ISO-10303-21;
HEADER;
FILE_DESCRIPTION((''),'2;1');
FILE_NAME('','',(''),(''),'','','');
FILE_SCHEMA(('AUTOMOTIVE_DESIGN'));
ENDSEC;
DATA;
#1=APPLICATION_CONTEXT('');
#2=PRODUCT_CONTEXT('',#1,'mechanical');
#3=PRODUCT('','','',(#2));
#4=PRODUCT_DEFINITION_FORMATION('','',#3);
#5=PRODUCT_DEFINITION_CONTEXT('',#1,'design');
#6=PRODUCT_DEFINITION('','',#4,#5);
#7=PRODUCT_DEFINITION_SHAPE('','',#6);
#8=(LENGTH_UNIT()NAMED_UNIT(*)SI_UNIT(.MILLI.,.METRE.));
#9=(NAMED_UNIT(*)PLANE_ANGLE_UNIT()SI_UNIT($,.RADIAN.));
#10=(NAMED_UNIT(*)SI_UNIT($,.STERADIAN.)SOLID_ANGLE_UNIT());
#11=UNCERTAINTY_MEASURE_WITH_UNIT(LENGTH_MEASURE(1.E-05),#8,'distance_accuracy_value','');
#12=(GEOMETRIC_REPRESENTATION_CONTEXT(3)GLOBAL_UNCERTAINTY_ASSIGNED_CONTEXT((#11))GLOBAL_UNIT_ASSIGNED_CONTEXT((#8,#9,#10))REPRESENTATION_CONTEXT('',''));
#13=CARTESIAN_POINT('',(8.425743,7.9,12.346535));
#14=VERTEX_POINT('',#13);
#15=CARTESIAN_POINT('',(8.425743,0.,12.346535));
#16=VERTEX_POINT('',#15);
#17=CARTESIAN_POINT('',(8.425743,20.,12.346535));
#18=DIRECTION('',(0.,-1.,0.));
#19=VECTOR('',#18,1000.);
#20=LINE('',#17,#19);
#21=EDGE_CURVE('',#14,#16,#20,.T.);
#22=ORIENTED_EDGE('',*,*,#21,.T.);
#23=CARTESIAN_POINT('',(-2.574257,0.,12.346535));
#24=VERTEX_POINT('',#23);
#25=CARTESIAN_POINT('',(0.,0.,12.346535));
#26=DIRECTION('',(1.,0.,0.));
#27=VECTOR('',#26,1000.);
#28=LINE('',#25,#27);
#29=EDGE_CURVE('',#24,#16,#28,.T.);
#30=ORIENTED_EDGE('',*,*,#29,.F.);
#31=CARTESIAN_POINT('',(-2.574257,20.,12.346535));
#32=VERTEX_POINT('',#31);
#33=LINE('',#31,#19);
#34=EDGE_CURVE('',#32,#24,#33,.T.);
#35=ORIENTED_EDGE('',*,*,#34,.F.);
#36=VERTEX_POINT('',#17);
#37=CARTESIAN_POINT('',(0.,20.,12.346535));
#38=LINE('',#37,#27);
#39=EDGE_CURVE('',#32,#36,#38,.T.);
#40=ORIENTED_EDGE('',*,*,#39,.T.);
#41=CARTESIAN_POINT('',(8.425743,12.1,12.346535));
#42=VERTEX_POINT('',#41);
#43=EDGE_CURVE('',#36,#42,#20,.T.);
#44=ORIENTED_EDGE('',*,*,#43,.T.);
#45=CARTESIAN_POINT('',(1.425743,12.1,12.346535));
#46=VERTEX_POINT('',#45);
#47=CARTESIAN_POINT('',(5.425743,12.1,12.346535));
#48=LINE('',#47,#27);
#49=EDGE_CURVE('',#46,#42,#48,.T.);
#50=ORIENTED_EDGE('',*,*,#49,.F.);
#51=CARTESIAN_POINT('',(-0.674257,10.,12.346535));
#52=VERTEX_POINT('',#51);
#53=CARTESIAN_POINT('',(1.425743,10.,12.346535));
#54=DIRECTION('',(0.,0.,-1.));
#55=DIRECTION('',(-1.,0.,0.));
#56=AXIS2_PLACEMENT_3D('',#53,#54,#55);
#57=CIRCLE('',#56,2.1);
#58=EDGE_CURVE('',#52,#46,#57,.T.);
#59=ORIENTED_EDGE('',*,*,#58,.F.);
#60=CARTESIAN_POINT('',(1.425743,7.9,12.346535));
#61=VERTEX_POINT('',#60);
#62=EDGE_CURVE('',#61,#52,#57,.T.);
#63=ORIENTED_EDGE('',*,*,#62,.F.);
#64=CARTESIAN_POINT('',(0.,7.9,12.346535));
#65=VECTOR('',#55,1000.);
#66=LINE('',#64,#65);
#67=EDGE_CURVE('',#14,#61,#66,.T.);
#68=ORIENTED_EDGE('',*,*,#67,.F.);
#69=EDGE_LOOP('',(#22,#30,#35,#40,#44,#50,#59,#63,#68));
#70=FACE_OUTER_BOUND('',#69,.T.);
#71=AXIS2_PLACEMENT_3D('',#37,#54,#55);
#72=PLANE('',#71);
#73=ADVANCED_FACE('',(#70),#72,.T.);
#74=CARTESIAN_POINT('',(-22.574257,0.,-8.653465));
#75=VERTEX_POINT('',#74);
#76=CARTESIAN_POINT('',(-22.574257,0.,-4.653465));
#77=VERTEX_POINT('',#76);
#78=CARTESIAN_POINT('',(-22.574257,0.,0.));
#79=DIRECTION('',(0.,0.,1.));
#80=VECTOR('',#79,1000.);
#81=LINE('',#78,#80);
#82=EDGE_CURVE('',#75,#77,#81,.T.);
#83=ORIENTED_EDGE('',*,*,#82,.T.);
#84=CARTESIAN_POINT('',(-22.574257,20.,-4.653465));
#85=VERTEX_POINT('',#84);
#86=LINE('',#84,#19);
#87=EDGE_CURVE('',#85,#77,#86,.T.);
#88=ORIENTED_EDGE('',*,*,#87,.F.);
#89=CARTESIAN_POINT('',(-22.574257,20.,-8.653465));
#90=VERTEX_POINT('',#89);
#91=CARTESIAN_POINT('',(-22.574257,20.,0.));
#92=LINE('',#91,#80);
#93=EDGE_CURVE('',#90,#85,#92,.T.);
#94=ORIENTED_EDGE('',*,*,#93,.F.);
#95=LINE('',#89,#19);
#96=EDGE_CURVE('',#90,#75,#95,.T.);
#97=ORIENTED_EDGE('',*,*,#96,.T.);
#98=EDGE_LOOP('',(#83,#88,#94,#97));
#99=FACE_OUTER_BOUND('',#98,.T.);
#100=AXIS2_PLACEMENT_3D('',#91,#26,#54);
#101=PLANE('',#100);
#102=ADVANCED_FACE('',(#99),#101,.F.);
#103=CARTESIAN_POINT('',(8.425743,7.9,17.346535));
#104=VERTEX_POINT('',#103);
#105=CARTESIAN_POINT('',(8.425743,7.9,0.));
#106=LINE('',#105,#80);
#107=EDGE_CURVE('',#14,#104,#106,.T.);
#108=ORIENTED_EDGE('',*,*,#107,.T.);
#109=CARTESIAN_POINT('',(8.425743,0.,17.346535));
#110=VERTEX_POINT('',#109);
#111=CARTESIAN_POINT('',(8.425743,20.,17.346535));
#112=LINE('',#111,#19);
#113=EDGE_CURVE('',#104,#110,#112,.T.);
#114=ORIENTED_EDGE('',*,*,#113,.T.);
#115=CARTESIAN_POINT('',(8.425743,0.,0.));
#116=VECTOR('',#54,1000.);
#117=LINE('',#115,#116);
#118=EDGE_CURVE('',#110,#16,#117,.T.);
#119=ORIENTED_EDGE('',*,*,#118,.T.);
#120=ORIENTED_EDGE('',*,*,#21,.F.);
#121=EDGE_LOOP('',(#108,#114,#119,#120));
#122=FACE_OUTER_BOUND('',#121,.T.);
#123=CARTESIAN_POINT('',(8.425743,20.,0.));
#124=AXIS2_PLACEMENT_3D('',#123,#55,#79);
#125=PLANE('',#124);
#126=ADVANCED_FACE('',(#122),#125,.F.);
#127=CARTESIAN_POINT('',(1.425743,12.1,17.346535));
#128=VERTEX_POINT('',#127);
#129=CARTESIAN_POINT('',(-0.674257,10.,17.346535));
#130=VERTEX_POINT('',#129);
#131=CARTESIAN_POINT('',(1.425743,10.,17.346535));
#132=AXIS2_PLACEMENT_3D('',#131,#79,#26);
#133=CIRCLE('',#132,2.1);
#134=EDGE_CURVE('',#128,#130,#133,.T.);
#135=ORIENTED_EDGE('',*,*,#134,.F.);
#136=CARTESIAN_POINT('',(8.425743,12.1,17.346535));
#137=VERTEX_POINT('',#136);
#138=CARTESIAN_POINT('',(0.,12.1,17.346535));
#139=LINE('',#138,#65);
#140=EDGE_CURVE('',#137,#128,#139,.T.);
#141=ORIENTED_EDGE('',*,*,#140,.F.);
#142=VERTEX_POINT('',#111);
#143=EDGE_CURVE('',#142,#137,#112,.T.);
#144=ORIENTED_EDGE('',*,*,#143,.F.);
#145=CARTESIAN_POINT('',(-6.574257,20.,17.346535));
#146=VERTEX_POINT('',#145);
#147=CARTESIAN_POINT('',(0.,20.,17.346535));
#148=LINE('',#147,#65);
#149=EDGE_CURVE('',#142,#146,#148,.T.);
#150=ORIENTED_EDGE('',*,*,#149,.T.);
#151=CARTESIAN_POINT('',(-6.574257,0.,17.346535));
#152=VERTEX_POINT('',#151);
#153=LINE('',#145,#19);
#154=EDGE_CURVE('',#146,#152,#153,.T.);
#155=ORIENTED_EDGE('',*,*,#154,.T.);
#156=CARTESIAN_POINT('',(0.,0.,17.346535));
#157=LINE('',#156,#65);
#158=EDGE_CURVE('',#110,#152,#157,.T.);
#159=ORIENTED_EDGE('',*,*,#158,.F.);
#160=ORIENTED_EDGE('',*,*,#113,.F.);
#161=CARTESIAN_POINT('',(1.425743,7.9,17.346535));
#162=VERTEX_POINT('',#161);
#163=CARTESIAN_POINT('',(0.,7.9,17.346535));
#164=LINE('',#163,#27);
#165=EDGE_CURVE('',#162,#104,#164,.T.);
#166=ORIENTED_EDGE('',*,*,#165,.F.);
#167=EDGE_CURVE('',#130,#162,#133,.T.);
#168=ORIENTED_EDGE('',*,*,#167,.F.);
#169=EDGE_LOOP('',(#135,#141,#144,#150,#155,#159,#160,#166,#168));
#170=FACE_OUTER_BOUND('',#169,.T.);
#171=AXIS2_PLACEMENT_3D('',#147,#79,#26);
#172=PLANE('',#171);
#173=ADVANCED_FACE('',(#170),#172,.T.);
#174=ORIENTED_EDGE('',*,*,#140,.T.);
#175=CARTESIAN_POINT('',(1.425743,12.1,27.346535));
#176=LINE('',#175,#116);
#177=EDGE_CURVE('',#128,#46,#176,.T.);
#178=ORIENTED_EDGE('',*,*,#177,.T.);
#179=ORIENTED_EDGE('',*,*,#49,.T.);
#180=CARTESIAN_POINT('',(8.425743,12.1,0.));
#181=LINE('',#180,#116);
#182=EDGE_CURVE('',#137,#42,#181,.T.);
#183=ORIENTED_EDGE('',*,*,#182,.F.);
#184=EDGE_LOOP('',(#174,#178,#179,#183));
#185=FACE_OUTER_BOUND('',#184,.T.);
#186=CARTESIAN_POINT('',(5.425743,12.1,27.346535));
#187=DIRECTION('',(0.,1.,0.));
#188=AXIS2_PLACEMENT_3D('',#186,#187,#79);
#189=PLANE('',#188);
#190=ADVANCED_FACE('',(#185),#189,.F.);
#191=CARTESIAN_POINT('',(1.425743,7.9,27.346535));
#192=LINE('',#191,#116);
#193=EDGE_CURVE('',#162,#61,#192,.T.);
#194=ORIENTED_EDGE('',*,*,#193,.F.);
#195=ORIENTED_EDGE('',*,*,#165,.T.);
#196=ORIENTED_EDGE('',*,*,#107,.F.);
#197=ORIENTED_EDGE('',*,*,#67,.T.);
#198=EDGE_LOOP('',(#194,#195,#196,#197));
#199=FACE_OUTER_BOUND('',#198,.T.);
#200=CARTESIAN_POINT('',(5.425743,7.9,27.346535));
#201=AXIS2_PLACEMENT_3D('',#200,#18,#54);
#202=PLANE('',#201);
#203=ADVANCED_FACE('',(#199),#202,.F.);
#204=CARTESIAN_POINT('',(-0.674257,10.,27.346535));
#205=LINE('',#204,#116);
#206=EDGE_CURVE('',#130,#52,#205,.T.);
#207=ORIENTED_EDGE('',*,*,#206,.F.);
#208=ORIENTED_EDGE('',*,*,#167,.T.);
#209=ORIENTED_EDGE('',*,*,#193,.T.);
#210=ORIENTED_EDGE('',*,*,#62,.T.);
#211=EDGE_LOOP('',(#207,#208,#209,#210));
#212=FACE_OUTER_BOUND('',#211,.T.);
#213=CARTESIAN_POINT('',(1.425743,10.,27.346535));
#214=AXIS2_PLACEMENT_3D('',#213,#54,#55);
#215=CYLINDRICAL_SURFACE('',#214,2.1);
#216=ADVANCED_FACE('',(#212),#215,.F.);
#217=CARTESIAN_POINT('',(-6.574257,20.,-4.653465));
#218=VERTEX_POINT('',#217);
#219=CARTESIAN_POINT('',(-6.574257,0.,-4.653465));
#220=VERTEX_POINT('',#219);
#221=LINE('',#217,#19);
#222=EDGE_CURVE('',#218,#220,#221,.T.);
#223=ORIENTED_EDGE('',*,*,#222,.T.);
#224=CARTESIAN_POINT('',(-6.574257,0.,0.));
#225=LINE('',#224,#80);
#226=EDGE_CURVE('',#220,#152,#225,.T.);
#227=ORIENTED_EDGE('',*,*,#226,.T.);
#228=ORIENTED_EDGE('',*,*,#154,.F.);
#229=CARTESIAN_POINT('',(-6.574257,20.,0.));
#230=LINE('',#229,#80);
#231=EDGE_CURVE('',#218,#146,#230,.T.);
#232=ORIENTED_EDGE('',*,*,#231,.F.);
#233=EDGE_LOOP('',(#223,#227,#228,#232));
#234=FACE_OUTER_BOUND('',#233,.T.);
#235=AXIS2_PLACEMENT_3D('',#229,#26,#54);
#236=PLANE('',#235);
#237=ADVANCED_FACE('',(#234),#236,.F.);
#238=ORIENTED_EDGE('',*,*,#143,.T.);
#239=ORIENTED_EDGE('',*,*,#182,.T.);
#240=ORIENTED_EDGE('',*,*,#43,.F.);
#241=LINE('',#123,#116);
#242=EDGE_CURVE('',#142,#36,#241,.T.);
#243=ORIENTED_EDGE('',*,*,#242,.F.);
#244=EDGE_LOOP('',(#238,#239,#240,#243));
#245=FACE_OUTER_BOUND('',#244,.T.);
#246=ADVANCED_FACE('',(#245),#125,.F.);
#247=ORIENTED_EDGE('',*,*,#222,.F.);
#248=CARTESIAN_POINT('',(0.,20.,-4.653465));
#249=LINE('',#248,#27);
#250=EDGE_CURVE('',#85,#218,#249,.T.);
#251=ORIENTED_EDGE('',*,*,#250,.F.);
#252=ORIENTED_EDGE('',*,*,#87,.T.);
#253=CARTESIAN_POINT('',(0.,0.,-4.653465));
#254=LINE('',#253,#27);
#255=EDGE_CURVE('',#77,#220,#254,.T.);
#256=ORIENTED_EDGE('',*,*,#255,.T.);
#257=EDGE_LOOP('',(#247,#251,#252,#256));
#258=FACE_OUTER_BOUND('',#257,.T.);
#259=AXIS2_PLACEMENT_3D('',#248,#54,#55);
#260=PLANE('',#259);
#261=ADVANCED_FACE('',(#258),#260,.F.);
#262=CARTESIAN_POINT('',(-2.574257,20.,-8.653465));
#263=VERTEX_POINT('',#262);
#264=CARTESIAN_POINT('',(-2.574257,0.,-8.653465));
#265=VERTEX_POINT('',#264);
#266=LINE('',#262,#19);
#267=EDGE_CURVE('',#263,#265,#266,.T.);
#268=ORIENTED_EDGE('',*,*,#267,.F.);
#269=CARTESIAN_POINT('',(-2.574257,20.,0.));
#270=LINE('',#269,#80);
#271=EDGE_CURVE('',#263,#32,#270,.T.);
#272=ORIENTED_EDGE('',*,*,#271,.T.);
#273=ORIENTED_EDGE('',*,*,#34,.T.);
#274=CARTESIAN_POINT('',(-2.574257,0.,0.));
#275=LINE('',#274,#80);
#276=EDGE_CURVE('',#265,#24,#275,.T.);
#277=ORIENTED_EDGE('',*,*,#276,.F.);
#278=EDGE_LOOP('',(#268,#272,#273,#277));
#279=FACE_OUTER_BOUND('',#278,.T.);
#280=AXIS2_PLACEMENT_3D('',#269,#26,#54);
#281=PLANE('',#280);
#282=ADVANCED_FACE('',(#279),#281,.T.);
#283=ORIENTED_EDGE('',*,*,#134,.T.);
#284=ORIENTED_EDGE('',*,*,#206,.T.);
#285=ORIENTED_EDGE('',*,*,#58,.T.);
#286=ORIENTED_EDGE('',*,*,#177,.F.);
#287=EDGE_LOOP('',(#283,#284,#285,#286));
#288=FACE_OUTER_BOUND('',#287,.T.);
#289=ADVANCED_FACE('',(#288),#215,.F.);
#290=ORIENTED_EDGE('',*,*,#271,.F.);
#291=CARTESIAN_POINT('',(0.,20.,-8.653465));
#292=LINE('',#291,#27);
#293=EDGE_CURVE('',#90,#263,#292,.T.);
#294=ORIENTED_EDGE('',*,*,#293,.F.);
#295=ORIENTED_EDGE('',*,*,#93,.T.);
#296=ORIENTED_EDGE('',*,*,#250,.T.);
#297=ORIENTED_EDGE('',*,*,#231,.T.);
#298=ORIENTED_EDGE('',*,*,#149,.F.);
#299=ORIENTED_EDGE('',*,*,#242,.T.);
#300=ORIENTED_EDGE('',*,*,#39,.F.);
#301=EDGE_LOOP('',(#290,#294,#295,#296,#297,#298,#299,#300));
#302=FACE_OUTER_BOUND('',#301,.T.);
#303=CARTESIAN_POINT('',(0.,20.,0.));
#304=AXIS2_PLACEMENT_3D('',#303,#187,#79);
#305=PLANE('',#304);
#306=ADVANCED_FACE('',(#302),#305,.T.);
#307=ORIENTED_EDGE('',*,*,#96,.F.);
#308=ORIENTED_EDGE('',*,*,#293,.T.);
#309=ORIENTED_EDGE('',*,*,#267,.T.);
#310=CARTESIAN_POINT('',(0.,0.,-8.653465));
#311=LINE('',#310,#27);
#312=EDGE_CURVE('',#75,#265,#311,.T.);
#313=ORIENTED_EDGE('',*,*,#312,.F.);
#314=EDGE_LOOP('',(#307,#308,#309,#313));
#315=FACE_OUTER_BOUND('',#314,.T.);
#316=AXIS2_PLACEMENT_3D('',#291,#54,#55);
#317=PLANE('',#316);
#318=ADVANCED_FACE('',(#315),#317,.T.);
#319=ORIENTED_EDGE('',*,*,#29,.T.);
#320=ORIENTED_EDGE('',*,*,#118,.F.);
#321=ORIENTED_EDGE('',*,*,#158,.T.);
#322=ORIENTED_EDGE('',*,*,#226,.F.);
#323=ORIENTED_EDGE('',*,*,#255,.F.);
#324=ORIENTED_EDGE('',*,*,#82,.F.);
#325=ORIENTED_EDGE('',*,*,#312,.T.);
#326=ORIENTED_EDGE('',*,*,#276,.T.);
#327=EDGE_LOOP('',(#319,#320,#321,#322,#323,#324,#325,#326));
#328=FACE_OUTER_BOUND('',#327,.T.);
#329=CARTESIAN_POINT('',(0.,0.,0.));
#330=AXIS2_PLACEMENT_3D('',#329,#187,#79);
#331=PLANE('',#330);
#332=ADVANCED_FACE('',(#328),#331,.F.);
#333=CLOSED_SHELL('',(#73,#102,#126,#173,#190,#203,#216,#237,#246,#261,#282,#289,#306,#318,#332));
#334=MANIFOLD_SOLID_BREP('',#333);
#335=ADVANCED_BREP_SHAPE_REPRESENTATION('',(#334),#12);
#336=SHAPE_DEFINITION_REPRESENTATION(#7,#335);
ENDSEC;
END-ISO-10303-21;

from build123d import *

# Parameters (mm, degrees)
SKETCH1_W           = 16
SKETCH1_H           = 4
SKETCH1_W_2         = 4
SKETCH1_H_2         = 17
SKETCH1_H_3         = 5
SKETCH1_W_3         = 11
BOSS_EXTRUDE1_DEPTH = 20
CUT_EXTRUDE1_DEPTH  = 15


with BuildPart() as part:
    # Sketch1 → Boss-Extrude1 (new body)
    with BuildSketch(Plane(origin=(0, 0, 0), x_dir=(1, 0, 0), z_dir=(0, 1, 0))):
        with Locations((-14.574257426, 6.653465347)):
            Rectangle(SKETCH1_W, SKETCH1_H)
        with Locations((-4.574257426, 6.653465347)):
            Rectangle(SKETCH1_W_2, SKETCH1_H)
        with Locations((-4.574257426, -3.846534653)):
            Rectangle(SKETCH1_W_2, SKETCH1_H_2)
        with Locations((-4.574257426, -14.846534653)):
            Rectangle(SKETCH1_W_2, SKETCH1_H_3)
        with Locations((2.925742574, -14.846534653)):
            Rectangle(SKETCH1_W_3, SKETCH1_H_3)
    extrude(amount=BOSS_EXTRUDE1_DEPTH)

    # Sketch2 → Cut-Extrude1 (cut)
    with BuildSketch(Plane(origin=(0, 0, 12.346534653), x_dir=(-1, 0, 0), z_dir=(0, 0, -1))):
        with BuildLine():
            Line((-5.425742574, 7.9), (-8.841676891, 7.9))
            Line((-8.841676891, 7.9), (-8.841676891, 11.852277474))
            Line((-8.841676891, 11.852277474), (-8.841676891, 12.1))
            Line((-8.841676891, 12.1), (-5.425742574, 12.1))
            Line((-5.425742574, 12.1), (-1.425742574, 12.1))
            ThreePointArc((-1.425742574, 12.1), (0.674257426, 10), (-1.425742574, 7.9))
            Line((-1.425742574, 7.9), (-5.425742574, 7.9))
        make_face()
    extrude(amount=-CUT_EXTRUDE1_DEPTH, mode=Mode.SUBTRACT)


solid = part.part
